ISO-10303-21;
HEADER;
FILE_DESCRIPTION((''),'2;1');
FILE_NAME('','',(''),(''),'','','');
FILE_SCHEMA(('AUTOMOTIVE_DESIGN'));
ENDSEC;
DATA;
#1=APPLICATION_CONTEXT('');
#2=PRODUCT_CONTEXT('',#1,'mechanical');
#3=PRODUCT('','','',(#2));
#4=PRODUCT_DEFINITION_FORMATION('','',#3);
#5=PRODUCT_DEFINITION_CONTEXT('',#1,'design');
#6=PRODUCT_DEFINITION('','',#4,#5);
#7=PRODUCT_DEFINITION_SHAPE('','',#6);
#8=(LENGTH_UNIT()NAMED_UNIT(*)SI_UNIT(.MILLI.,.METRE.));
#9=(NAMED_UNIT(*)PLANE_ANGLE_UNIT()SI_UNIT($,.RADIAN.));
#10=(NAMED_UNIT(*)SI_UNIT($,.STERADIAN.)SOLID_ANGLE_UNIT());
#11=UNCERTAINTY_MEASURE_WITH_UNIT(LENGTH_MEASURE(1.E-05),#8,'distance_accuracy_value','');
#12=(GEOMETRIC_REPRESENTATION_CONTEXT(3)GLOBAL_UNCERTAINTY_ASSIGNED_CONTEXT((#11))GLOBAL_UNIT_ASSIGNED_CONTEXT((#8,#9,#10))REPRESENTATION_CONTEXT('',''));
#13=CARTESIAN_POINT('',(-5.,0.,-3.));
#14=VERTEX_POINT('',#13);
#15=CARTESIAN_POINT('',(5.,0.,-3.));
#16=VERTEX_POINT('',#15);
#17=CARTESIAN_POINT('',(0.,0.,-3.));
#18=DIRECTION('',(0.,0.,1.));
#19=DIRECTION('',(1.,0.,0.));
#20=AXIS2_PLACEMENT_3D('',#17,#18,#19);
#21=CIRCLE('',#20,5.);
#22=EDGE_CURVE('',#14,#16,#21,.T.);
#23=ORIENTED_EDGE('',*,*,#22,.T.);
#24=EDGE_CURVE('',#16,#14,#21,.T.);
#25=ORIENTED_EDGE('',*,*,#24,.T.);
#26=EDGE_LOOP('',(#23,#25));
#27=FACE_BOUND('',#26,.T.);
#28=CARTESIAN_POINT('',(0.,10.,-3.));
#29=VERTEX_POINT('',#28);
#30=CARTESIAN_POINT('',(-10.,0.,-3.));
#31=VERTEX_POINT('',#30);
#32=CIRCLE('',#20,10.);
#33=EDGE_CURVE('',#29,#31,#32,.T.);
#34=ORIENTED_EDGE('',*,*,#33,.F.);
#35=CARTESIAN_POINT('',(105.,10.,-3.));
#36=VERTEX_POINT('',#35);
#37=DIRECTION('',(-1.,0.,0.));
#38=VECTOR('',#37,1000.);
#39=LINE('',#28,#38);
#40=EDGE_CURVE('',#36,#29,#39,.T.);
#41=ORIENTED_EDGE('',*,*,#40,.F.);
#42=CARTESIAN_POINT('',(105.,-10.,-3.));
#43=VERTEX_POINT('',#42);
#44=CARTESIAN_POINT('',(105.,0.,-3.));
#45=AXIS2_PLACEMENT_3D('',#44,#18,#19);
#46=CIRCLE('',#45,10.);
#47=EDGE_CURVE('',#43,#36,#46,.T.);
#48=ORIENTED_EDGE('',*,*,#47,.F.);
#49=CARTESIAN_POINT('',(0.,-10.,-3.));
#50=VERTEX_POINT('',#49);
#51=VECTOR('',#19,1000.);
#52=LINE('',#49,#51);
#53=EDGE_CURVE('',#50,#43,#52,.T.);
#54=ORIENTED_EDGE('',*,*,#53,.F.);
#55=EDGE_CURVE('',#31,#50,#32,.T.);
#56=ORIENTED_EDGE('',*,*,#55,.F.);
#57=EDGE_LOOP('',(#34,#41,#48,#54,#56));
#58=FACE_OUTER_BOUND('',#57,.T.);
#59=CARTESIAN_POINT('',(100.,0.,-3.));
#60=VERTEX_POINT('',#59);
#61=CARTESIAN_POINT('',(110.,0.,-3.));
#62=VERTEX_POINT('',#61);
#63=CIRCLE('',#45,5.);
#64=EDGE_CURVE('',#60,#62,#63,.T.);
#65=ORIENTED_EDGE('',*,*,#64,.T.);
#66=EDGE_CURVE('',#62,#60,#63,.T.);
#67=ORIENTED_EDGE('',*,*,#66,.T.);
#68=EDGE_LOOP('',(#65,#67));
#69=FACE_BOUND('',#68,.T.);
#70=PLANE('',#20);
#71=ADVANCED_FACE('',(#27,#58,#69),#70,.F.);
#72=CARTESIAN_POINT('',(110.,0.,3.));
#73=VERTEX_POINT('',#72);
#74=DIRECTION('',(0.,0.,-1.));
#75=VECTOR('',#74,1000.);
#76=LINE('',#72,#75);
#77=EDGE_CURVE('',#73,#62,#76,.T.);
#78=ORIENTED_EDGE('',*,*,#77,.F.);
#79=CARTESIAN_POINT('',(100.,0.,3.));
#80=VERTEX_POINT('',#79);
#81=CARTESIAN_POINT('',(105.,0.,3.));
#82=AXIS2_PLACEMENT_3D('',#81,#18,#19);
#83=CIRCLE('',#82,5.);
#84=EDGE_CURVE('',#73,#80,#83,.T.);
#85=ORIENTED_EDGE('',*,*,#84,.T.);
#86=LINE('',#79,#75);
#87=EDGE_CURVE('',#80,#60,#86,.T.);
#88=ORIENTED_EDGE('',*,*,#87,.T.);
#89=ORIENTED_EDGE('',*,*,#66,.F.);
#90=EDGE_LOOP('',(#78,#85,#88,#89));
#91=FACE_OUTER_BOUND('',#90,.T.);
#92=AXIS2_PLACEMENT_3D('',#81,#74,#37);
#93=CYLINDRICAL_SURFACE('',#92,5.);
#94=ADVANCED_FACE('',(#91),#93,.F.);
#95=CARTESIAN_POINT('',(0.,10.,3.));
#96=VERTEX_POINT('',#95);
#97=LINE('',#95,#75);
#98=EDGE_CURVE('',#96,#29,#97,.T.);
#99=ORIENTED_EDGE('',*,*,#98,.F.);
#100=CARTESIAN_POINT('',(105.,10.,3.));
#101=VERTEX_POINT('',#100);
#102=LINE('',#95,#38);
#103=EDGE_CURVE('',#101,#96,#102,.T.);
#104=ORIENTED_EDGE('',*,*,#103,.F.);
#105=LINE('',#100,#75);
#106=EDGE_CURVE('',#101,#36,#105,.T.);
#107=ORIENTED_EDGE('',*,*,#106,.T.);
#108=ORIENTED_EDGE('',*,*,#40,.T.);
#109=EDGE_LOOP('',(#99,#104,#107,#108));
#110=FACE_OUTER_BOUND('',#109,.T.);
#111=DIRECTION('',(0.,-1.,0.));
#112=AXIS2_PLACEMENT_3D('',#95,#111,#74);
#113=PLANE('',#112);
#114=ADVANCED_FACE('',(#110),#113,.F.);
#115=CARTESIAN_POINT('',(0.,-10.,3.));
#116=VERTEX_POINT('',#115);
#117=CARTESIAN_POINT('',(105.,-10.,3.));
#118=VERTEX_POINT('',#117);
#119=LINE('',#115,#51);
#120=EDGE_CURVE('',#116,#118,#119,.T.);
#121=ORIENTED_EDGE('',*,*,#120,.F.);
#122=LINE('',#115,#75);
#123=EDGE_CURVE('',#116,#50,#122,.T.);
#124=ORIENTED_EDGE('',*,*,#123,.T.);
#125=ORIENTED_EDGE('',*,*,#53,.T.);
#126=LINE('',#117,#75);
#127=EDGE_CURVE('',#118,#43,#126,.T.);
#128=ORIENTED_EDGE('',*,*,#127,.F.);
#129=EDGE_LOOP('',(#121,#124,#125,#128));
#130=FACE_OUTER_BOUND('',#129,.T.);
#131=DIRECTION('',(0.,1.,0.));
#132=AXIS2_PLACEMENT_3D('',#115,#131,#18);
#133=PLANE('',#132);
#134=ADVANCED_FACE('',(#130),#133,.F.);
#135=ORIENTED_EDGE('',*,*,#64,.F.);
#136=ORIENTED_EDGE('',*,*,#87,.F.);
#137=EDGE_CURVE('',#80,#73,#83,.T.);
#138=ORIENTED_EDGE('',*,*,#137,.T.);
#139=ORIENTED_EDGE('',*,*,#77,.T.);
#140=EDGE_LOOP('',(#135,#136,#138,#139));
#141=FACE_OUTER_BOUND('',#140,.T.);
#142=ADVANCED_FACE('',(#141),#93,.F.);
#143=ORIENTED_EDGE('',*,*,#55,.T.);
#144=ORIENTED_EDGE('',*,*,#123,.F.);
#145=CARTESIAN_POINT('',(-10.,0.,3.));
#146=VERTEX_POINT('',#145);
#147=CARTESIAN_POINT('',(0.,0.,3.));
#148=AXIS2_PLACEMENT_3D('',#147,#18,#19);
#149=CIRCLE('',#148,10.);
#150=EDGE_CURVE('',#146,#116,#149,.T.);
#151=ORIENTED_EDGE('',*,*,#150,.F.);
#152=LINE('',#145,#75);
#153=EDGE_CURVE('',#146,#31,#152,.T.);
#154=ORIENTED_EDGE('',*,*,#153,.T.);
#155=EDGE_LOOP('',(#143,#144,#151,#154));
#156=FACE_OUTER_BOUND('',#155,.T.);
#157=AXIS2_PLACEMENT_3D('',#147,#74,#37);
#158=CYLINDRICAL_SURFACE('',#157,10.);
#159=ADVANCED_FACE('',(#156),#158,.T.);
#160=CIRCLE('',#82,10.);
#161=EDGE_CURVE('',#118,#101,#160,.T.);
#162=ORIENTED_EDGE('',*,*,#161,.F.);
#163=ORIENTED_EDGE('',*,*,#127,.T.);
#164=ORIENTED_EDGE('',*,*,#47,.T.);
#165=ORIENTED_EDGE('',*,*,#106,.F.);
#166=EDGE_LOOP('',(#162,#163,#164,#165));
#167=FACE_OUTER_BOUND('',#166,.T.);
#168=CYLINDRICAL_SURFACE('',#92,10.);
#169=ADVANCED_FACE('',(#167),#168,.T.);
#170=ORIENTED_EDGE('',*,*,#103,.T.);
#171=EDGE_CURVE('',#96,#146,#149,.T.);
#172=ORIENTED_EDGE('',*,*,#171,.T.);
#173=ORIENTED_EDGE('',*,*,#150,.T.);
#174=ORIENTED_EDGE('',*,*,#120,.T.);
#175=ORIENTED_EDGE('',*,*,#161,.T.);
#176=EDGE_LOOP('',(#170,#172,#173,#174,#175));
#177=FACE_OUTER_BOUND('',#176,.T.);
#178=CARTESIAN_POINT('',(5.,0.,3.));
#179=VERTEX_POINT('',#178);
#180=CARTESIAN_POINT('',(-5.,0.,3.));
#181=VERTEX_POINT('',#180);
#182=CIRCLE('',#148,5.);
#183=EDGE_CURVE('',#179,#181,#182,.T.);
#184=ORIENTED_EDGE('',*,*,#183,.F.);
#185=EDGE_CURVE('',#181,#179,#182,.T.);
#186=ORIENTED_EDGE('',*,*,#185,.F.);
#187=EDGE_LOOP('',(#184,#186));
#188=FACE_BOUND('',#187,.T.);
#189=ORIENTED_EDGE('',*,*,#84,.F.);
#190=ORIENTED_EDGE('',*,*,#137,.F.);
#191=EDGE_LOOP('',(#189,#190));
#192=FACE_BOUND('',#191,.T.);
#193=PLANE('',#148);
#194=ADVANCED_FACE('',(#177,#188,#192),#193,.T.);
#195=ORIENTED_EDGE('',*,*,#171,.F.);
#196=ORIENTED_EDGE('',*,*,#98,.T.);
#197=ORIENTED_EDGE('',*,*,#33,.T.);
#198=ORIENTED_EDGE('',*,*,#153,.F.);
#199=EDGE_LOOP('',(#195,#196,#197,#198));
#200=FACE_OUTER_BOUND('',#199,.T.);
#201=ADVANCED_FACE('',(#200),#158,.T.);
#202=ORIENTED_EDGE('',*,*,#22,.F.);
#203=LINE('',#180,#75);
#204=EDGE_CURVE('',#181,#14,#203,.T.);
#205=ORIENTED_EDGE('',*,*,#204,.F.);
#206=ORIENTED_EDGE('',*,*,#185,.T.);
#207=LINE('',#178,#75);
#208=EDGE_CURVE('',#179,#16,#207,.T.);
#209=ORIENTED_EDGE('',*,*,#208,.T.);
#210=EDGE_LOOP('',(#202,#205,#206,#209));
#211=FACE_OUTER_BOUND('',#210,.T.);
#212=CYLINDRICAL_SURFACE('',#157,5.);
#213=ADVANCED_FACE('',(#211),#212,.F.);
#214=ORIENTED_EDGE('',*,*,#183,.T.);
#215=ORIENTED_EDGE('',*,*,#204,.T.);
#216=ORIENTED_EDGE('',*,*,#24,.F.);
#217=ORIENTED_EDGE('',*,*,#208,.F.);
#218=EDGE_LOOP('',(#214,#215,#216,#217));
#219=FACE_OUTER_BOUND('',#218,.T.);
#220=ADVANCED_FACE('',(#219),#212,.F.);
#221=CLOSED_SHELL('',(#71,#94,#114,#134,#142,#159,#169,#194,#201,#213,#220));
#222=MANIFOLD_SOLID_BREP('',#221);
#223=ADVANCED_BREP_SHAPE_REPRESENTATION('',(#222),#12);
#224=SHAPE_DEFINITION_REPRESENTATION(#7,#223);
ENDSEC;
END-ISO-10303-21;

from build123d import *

# Parameters (mm, degrees)
SKETCH1_R           = 5
BOSS_EXTRUDE1_DEPTH = 3


with BuildPart() as part:
    # Sketch1 → Boss-Extrude1 (new, symmetric)
    with BuildSketch(Plane.XY):
        with BuildLine():
            Line((0, 10), (105, 10))
            ThreePointArc((105, 10), (115, 0), (105, -10))
            Line((105, -10), (0, -10))
            ThreePointArc((0, -10), (-10, 0), (0, 10))
        make_face()
        Circle(SKETCH1_R, mode=Mode.SUBTRACT)
        with Locations((105, 0)):
            Circle(SKETCH1_R, mode=Mode.SUBTRACT)
    extrude(amount=BOSS_EXTRUDE1_DEPTH, both=True)


solid = part.part
